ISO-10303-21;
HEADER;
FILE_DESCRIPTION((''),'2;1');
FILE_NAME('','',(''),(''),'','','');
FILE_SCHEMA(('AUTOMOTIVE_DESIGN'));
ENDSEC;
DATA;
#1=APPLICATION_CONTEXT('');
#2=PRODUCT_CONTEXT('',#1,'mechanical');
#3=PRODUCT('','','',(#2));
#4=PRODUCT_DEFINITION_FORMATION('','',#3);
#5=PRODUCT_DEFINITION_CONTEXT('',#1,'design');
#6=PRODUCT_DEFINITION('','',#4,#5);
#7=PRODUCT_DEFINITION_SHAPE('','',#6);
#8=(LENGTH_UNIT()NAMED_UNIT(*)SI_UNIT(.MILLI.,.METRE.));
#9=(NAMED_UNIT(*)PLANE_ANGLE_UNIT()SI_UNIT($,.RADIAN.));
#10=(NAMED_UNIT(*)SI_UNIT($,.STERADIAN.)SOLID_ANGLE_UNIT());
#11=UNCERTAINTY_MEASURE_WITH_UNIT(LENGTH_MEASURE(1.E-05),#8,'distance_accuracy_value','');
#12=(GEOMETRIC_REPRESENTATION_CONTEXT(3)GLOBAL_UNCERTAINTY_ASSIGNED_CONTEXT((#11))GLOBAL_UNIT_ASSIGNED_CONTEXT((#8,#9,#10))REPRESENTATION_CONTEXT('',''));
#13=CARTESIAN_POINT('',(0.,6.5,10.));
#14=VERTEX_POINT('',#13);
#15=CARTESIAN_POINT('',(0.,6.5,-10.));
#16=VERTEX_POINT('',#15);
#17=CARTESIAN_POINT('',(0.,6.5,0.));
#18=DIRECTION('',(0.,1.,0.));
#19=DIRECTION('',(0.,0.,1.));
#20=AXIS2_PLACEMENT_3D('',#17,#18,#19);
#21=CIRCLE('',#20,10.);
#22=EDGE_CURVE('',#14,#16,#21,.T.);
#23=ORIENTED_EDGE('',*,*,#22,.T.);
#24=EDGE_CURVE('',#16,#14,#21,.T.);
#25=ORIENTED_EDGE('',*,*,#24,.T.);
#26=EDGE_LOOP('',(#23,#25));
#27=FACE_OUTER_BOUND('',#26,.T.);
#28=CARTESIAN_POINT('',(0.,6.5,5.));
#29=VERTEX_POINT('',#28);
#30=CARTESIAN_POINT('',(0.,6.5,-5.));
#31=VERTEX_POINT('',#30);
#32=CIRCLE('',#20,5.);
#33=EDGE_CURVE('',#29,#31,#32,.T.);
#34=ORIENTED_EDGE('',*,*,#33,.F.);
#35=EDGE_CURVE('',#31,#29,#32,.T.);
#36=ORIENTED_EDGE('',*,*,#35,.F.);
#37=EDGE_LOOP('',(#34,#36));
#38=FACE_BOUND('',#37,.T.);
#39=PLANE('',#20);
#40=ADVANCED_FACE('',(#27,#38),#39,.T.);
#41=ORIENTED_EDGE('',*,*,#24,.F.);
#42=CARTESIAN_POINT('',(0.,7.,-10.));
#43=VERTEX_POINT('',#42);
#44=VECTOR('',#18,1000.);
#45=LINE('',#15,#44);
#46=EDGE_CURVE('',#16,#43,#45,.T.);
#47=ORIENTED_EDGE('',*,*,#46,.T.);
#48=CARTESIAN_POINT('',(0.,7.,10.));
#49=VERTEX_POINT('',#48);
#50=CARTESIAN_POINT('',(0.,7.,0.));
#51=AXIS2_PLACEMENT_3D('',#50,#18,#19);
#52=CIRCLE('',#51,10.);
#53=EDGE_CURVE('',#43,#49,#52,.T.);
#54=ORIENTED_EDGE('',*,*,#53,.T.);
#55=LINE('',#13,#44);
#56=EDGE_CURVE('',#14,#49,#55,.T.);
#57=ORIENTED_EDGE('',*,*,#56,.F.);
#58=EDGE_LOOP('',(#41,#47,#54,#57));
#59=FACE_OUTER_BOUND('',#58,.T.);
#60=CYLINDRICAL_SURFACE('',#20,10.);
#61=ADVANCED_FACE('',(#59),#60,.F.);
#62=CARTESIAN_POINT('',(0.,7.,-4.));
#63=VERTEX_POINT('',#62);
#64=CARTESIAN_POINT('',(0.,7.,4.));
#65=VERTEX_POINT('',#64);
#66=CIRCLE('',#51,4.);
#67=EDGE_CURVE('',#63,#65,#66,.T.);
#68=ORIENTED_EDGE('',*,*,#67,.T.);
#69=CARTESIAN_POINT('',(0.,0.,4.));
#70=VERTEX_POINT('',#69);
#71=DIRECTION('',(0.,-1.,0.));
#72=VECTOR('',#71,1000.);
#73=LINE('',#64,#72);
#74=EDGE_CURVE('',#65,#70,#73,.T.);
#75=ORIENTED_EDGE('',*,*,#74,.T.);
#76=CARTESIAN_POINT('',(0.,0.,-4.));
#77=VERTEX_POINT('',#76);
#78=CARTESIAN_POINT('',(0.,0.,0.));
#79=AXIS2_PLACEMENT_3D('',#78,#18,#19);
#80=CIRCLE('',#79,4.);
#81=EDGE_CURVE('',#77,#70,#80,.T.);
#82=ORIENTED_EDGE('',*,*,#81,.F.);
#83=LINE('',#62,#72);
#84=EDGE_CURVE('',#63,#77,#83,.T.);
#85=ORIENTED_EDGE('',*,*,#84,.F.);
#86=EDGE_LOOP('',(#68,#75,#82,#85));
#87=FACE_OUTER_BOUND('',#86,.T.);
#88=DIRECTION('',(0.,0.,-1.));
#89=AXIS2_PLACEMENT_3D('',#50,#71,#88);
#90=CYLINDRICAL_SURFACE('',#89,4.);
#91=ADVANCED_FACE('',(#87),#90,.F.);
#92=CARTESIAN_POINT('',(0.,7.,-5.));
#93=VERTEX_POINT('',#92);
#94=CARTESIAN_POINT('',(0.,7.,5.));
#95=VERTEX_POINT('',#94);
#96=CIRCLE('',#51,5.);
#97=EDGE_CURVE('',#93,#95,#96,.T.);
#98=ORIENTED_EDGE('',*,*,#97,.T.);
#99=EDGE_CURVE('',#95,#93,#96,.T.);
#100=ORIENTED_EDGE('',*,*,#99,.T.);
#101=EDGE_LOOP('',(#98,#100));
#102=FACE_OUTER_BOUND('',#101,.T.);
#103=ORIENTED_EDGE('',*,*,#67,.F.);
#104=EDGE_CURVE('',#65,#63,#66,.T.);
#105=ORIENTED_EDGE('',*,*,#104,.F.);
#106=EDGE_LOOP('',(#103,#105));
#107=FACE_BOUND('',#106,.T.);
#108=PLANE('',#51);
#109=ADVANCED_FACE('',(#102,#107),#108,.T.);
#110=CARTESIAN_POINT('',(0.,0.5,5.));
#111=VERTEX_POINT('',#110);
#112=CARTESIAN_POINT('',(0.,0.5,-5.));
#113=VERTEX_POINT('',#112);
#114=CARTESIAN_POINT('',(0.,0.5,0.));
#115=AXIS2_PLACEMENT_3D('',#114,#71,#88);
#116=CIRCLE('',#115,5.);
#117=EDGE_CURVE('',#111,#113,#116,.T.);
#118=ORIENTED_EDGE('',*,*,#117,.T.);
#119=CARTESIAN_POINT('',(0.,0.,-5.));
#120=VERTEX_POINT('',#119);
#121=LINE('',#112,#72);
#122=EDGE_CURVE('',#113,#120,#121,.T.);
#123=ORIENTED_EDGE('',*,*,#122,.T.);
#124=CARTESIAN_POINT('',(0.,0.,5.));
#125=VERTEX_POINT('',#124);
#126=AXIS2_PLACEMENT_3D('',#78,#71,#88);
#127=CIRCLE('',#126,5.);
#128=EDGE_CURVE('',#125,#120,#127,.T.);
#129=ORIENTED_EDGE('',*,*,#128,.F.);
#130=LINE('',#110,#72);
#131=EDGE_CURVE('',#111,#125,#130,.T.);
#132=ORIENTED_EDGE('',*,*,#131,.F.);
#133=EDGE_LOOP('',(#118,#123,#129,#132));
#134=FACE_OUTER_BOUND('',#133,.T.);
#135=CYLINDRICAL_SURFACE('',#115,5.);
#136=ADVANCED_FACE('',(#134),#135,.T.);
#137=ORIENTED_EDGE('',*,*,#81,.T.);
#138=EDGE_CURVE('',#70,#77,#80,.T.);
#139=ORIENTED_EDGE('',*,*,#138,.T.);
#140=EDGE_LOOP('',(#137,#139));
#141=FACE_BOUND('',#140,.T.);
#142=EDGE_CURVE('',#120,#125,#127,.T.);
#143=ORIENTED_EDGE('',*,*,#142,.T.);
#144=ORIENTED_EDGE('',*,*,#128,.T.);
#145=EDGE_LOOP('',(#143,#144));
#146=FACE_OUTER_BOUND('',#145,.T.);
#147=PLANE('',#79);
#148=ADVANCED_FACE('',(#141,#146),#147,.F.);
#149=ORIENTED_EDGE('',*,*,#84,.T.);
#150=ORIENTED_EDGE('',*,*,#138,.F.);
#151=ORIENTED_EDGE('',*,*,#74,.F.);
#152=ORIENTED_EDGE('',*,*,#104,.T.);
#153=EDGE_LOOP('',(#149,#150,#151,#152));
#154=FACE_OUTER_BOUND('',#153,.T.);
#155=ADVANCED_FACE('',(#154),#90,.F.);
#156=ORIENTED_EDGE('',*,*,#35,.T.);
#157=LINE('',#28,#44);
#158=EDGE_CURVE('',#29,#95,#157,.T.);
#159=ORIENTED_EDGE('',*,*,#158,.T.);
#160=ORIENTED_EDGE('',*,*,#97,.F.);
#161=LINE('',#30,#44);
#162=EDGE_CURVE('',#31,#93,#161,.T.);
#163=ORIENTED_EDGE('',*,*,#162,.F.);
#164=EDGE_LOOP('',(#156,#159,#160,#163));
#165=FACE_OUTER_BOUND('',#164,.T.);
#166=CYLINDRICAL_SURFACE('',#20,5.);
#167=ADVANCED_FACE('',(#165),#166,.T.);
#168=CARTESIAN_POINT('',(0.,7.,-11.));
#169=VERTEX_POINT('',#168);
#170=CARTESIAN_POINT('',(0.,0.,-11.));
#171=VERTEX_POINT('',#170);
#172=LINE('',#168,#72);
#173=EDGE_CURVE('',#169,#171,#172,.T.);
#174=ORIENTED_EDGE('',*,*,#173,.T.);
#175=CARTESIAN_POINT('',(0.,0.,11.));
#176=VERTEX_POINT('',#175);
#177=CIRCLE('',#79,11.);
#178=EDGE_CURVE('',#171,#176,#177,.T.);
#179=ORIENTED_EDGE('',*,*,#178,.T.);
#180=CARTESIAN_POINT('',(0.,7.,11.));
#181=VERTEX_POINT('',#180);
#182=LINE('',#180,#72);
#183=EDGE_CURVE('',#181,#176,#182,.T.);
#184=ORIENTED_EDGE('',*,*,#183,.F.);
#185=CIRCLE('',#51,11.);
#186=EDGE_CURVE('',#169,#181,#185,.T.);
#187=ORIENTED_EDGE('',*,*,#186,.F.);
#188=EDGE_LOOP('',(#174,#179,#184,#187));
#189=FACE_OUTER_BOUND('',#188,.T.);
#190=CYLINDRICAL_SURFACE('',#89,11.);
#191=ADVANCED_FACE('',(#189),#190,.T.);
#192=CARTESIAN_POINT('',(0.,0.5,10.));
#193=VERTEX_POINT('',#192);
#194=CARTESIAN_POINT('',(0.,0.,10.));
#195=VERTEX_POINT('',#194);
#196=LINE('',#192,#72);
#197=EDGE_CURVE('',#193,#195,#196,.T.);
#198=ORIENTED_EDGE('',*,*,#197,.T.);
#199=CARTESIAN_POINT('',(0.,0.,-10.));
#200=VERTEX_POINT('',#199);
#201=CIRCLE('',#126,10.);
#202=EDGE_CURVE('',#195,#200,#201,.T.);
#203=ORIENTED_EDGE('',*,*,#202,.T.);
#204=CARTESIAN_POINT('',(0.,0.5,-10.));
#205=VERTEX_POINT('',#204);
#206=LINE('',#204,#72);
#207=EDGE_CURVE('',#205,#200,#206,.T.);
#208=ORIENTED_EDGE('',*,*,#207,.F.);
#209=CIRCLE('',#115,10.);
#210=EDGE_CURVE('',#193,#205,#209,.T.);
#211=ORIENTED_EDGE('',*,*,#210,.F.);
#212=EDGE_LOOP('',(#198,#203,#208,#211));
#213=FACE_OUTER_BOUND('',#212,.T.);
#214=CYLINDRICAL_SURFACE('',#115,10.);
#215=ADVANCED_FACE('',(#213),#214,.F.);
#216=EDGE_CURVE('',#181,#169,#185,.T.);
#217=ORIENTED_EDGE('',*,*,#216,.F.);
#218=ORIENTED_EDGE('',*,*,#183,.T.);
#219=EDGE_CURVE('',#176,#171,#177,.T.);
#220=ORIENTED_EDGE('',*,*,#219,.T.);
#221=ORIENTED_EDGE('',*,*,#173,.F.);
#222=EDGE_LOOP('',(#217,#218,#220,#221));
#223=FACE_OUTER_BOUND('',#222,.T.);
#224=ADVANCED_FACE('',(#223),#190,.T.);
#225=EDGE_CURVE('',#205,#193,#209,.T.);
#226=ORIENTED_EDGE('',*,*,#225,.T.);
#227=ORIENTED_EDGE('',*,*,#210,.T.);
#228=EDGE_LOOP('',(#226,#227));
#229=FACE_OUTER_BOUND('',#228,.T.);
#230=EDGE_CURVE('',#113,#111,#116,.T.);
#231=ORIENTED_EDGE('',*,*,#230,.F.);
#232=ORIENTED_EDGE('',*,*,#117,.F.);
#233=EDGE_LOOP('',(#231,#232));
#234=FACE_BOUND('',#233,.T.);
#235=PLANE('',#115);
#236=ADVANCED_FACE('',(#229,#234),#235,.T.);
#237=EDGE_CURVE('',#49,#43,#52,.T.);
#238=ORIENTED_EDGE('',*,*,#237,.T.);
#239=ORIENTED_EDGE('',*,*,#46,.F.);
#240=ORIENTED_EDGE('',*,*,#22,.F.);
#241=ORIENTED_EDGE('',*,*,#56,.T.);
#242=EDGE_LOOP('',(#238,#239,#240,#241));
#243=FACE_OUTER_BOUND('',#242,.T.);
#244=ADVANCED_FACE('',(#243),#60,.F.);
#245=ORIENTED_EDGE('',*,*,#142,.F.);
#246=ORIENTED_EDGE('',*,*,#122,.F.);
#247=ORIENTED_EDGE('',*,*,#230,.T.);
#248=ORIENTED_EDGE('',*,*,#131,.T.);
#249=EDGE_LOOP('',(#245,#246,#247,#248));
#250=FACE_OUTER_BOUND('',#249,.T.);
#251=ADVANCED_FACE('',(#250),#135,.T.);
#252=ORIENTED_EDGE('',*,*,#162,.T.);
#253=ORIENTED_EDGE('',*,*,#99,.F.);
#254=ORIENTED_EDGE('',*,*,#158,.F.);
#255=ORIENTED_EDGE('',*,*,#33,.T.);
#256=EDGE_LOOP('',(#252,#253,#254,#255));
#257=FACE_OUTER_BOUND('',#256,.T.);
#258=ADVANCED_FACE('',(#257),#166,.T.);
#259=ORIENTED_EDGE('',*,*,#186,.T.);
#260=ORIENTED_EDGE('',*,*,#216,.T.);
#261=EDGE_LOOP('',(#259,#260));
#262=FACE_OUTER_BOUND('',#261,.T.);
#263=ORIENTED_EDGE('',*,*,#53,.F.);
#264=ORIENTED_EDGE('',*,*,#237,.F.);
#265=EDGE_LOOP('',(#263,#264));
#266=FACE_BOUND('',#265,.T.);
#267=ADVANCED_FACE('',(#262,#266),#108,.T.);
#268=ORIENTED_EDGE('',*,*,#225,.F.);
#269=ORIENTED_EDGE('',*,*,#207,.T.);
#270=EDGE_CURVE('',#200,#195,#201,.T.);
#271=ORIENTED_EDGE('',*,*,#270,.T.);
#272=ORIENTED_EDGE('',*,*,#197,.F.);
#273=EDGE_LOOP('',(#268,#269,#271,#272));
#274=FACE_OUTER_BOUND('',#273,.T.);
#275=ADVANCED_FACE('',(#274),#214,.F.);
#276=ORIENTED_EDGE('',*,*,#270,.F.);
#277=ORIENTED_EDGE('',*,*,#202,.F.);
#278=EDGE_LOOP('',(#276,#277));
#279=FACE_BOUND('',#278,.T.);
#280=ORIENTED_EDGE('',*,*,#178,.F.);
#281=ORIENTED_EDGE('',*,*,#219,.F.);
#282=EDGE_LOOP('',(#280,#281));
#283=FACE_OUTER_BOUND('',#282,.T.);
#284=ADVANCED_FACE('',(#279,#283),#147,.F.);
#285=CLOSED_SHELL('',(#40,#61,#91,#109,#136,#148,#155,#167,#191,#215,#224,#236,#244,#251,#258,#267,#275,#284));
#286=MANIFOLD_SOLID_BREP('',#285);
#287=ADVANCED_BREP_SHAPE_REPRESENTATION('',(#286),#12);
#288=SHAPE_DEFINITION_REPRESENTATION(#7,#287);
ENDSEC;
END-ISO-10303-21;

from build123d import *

# Parameters (mm, degrees)
SKETCH1_R           = 11
SKETCH1_R_2         = 4
BOSS_EXTRUDE1_DEPTH = 7
SKETCH2_R           = 10
SKETCH2_R_2         = 5
CUT_EXTRUDE1_DEPTH  = 0.5
CUT_EXTRUDE2_START  = -0.5
SKETCH3_R           = 10
SKETCH3_R_2         = 5
CUT_EXTRUDE2_DEPTH  = 0.5


with BuildPart() as part:
    # Sketch1 → Boss-Extrude1 (new body)
    with BuildSketch(Plane(origin=(0, 0, 0), x_dir=(1, 0, 0), z_dir=(0, 1, 0))):
        with Locations(Location((0, 0, 0), (0, 0, 270))):
            Circle(SKETCH1_R)
        with Locations(Location((0, 0, 0), (0, 0, 270))):
            Circle(SKETCH1_R_2, mode=Mode.SUBTRACT)
    extrude(amount=BOSS_EXTRUDE1_DEPTH)

    # Sketch2 → Cut-Extrude1 (cut)
    with BuildSketch(Plane.XZ):
        with Locations(Location((0, 0, 0), (0, 0, 270))):
            Circle(SKETCH2_R)
        with Locations(Location((0, 0, 0), (0, 0, 270))):
            Circle(SKETCH2_R_2, mode=Mode.SUBTRACT)
    extrude(amount=-CUT_EXTRUDE1_DEPTH, mode=Mode.SUBTRACT)

    # Sketch3 → Cut-Extrude2 (cut)
    with BuildSketch(Plane(origin=(0, 7, 0), x_dir=(1, 0, 0), z_dir=(0, 1, 0)).offset(CUT_EXTRUDE2_START)):
        with Locations(Location((0, 0, 0), (0, 0, 90))):
            Circle(SKETCH3_R)
        with Locations(Location((0, 0, 0), (0, 0, 90))):
            Circle(SKETCH3_R_2, mode=Mode.SUBTRACT)
    extrude(amount=CUT_EXTRUDE2_DEPTH, mode=Mode.SUBTRACT)


solid = part.part
